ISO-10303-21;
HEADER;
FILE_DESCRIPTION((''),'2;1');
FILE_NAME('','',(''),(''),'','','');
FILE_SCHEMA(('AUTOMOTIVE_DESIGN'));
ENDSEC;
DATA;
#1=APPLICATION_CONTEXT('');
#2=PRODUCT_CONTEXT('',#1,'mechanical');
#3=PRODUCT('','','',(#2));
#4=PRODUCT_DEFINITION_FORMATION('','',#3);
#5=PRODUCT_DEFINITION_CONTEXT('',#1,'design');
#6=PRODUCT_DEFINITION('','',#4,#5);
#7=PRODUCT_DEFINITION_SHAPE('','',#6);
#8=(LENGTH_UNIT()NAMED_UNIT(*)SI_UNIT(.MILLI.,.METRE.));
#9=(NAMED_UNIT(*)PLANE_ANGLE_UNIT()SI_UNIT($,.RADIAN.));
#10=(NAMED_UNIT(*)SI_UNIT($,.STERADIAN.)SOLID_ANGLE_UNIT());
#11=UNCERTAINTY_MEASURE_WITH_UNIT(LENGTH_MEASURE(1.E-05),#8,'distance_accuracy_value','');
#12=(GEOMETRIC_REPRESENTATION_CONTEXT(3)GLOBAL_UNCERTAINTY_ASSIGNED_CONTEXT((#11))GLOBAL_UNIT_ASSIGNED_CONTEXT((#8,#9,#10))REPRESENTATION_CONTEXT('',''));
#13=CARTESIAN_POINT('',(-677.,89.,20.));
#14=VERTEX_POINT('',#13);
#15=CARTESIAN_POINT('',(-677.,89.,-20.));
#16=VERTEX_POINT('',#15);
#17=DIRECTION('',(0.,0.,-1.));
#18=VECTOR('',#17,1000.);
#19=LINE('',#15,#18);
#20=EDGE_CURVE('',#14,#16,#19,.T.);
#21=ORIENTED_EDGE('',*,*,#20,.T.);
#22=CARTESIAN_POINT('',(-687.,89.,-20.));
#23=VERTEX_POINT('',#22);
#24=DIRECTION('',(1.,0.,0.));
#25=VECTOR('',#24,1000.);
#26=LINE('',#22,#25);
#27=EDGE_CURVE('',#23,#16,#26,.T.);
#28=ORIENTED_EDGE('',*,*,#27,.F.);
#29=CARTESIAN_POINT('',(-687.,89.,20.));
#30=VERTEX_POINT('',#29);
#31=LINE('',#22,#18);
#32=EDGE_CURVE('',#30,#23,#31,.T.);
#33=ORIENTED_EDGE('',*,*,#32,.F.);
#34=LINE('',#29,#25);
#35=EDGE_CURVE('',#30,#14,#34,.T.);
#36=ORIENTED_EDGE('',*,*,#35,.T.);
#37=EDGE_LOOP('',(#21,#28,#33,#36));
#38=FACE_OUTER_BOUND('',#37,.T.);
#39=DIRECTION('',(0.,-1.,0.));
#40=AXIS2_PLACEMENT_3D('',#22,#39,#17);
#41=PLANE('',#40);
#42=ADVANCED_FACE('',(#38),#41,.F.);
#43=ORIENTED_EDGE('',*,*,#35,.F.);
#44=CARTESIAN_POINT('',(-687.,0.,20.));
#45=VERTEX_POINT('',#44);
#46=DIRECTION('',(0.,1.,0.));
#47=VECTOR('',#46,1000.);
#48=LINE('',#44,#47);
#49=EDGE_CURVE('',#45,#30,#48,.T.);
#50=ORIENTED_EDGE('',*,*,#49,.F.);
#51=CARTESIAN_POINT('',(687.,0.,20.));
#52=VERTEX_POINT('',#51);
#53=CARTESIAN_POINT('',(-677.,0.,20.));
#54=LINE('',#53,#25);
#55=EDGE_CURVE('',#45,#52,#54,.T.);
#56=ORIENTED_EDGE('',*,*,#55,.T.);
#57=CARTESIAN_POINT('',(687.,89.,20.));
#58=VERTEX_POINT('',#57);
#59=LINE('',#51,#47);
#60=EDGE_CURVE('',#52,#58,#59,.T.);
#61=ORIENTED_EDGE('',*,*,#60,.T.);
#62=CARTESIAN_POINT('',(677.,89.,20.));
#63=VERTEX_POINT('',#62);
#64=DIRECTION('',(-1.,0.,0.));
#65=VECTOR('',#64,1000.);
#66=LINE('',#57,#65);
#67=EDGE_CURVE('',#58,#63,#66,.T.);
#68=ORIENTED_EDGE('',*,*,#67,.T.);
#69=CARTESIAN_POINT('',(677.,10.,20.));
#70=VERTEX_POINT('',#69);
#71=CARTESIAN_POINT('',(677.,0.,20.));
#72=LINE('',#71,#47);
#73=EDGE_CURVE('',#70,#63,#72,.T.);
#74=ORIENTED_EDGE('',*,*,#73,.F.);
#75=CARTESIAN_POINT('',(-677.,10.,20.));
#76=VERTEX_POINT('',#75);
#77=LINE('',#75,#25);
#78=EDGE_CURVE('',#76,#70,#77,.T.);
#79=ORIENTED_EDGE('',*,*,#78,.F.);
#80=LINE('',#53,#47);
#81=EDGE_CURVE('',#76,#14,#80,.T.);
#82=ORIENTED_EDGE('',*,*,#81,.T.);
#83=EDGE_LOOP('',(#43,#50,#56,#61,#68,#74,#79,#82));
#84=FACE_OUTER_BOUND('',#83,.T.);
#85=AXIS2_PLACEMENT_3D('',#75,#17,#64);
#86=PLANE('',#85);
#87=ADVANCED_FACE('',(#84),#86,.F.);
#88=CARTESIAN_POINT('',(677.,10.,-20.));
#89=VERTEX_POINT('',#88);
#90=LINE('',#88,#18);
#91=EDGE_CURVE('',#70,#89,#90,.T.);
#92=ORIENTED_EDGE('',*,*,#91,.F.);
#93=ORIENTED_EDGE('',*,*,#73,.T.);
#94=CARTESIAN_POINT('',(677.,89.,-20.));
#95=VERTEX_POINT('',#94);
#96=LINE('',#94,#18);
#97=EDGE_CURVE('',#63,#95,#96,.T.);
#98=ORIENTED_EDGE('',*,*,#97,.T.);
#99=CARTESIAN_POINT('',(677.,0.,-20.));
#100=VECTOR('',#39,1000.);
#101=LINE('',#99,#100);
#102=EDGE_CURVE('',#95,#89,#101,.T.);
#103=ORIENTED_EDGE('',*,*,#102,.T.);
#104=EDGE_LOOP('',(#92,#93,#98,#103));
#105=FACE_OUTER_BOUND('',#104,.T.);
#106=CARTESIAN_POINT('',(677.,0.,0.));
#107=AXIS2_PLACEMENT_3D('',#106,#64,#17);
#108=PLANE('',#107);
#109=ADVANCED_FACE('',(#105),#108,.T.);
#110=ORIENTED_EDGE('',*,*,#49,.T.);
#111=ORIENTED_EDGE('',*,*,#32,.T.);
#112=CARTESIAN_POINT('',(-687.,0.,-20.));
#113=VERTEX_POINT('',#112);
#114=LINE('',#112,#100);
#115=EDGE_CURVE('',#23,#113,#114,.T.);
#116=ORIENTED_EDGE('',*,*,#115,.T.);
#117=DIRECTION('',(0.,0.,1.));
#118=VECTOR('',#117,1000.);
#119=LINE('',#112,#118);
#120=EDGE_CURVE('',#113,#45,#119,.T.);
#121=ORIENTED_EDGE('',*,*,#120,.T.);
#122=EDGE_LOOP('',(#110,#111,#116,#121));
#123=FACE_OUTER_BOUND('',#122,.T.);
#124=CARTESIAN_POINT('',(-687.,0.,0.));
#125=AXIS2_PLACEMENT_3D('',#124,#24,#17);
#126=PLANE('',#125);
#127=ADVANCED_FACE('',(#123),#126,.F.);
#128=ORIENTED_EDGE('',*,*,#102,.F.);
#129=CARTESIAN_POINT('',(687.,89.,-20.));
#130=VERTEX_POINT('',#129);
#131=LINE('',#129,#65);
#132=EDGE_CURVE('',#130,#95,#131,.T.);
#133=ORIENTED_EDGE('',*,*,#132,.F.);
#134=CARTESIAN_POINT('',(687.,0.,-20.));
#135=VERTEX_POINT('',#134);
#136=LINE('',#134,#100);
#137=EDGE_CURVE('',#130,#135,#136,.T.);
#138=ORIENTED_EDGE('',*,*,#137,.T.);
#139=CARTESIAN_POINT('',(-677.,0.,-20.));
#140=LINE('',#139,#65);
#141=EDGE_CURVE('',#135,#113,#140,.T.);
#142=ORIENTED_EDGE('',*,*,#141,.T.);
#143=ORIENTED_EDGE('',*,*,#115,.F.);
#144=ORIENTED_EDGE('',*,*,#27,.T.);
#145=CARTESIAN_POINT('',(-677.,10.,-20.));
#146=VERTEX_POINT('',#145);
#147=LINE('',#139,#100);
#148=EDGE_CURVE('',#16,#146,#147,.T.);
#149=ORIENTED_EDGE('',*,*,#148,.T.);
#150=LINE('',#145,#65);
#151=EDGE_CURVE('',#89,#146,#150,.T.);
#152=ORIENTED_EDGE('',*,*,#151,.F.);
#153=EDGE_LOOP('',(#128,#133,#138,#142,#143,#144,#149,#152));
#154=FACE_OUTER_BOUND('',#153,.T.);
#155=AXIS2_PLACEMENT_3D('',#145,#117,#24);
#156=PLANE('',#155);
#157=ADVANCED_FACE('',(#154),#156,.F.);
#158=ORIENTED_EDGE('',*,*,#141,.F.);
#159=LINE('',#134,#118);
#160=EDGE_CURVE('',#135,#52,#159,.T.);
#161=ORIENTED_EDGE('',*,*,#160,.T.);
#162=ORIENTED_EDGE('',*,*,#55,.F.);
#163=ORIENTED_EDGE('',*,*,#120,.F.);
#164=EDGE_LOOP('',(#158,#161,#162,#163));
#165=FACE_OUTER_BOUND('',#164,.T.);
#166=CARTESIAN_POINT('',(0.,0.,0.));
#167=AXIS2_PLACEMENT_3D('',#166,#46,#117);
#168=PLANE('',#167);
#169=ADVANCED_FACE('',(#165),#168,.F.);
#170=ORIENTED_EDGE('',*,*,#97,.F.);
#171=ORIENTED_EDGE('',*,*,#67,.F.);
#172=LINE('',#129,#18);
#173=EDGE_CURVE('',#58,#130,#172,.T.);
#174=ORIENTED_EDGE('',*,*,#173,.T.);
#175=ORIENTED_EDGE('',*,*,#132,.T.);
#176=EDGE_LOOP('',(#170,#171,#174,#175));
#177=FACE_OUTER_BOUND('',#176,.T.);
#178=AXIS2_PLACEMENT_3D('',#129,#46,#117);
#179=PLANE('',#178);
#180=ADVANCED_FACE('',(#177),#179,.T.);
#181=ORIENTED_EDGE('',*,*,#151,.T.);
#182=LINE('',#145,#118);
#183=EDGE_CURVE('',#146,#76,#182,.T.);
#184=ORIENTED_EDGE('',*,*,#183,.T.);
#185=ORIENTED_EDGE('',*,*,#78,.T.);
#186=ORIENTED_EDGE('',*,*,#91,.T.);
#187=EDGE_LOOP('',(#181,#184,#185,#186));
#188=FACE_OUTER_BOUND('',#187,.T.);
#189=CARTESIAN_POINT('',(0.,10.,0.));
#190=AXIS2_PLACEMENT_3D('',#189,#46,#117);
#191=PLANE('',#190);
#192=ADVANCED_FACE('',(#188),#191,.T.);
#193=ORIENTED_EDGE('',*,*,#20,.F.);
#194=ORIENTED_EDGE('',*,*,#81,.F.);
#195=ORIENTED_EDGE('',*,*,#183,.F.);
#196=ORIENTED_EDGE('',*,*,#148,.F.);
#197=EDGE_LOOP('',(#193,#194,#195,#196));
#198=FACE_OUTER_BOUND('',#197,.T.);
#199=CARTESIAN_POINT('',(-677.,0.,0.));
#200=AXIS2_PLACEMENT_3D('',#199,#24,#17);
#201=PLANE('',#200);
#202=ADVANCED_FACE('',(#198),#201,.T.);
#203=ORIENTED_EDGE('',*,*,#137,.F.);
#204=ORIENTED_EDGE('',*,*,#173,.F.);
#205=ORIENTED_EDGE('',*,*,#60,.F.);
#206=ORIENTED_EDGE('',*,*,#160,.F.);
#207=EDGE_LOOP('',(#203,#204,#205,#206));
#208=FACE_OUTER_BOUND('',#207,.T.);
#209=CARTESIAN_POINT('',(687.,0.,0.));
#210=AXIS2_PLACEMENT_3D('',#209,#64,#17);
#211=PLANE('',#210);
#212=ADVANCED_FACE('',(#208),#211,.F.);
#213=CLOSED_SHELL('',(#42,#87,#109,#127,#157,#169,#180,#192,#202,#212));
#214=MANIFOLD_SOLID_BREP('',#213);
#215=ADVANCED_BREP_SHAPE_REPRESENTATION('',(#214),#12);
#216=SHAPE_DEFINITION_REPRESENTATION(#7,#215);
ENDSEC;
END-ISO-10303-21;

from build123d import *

# Parameters (mm, degrees)
SKETCH_1_W      = 1354
SKETCH_1_H      = 40
EXTRUDE_1_DEPTH = 10
SKETCH_2_W      = 40
SKETCH_2_H      = 89
EXTRUDE_2_DEPTH = 10


with BuildPart() as part:
    # 草图1 → 凸台-拉伸1 (new body)
    with BuildSketch(Plane(origin=(0, 0, 0), x_dir=(1, 0, 0), z_dir=(0, 1, 0))):
        Rectangle(SKETCH_1_W, SKETCH_1_H)
    extrude(amount=EXTRUDE_1_DEPTH)

    # 草图2 → 凸台-拉伸2 (add)
    with BuildSketch(Plane.ZY.offset(677)):
        with Locations((0, 44.5)):
            Rectangle(SKETCH_2_W, SKETCH_2_H)
    extrude_2 = extrude(amount=EXTRUDE_2_DEPTH)

    # 镜向1: 凸台-拉伸2 across plane
    add(extrude_2.mirror(Plane(origin=(0, 0, 0), x_dir=(0, 0, 1), z_dir=(1, 0, 0))))


solid = part.part
